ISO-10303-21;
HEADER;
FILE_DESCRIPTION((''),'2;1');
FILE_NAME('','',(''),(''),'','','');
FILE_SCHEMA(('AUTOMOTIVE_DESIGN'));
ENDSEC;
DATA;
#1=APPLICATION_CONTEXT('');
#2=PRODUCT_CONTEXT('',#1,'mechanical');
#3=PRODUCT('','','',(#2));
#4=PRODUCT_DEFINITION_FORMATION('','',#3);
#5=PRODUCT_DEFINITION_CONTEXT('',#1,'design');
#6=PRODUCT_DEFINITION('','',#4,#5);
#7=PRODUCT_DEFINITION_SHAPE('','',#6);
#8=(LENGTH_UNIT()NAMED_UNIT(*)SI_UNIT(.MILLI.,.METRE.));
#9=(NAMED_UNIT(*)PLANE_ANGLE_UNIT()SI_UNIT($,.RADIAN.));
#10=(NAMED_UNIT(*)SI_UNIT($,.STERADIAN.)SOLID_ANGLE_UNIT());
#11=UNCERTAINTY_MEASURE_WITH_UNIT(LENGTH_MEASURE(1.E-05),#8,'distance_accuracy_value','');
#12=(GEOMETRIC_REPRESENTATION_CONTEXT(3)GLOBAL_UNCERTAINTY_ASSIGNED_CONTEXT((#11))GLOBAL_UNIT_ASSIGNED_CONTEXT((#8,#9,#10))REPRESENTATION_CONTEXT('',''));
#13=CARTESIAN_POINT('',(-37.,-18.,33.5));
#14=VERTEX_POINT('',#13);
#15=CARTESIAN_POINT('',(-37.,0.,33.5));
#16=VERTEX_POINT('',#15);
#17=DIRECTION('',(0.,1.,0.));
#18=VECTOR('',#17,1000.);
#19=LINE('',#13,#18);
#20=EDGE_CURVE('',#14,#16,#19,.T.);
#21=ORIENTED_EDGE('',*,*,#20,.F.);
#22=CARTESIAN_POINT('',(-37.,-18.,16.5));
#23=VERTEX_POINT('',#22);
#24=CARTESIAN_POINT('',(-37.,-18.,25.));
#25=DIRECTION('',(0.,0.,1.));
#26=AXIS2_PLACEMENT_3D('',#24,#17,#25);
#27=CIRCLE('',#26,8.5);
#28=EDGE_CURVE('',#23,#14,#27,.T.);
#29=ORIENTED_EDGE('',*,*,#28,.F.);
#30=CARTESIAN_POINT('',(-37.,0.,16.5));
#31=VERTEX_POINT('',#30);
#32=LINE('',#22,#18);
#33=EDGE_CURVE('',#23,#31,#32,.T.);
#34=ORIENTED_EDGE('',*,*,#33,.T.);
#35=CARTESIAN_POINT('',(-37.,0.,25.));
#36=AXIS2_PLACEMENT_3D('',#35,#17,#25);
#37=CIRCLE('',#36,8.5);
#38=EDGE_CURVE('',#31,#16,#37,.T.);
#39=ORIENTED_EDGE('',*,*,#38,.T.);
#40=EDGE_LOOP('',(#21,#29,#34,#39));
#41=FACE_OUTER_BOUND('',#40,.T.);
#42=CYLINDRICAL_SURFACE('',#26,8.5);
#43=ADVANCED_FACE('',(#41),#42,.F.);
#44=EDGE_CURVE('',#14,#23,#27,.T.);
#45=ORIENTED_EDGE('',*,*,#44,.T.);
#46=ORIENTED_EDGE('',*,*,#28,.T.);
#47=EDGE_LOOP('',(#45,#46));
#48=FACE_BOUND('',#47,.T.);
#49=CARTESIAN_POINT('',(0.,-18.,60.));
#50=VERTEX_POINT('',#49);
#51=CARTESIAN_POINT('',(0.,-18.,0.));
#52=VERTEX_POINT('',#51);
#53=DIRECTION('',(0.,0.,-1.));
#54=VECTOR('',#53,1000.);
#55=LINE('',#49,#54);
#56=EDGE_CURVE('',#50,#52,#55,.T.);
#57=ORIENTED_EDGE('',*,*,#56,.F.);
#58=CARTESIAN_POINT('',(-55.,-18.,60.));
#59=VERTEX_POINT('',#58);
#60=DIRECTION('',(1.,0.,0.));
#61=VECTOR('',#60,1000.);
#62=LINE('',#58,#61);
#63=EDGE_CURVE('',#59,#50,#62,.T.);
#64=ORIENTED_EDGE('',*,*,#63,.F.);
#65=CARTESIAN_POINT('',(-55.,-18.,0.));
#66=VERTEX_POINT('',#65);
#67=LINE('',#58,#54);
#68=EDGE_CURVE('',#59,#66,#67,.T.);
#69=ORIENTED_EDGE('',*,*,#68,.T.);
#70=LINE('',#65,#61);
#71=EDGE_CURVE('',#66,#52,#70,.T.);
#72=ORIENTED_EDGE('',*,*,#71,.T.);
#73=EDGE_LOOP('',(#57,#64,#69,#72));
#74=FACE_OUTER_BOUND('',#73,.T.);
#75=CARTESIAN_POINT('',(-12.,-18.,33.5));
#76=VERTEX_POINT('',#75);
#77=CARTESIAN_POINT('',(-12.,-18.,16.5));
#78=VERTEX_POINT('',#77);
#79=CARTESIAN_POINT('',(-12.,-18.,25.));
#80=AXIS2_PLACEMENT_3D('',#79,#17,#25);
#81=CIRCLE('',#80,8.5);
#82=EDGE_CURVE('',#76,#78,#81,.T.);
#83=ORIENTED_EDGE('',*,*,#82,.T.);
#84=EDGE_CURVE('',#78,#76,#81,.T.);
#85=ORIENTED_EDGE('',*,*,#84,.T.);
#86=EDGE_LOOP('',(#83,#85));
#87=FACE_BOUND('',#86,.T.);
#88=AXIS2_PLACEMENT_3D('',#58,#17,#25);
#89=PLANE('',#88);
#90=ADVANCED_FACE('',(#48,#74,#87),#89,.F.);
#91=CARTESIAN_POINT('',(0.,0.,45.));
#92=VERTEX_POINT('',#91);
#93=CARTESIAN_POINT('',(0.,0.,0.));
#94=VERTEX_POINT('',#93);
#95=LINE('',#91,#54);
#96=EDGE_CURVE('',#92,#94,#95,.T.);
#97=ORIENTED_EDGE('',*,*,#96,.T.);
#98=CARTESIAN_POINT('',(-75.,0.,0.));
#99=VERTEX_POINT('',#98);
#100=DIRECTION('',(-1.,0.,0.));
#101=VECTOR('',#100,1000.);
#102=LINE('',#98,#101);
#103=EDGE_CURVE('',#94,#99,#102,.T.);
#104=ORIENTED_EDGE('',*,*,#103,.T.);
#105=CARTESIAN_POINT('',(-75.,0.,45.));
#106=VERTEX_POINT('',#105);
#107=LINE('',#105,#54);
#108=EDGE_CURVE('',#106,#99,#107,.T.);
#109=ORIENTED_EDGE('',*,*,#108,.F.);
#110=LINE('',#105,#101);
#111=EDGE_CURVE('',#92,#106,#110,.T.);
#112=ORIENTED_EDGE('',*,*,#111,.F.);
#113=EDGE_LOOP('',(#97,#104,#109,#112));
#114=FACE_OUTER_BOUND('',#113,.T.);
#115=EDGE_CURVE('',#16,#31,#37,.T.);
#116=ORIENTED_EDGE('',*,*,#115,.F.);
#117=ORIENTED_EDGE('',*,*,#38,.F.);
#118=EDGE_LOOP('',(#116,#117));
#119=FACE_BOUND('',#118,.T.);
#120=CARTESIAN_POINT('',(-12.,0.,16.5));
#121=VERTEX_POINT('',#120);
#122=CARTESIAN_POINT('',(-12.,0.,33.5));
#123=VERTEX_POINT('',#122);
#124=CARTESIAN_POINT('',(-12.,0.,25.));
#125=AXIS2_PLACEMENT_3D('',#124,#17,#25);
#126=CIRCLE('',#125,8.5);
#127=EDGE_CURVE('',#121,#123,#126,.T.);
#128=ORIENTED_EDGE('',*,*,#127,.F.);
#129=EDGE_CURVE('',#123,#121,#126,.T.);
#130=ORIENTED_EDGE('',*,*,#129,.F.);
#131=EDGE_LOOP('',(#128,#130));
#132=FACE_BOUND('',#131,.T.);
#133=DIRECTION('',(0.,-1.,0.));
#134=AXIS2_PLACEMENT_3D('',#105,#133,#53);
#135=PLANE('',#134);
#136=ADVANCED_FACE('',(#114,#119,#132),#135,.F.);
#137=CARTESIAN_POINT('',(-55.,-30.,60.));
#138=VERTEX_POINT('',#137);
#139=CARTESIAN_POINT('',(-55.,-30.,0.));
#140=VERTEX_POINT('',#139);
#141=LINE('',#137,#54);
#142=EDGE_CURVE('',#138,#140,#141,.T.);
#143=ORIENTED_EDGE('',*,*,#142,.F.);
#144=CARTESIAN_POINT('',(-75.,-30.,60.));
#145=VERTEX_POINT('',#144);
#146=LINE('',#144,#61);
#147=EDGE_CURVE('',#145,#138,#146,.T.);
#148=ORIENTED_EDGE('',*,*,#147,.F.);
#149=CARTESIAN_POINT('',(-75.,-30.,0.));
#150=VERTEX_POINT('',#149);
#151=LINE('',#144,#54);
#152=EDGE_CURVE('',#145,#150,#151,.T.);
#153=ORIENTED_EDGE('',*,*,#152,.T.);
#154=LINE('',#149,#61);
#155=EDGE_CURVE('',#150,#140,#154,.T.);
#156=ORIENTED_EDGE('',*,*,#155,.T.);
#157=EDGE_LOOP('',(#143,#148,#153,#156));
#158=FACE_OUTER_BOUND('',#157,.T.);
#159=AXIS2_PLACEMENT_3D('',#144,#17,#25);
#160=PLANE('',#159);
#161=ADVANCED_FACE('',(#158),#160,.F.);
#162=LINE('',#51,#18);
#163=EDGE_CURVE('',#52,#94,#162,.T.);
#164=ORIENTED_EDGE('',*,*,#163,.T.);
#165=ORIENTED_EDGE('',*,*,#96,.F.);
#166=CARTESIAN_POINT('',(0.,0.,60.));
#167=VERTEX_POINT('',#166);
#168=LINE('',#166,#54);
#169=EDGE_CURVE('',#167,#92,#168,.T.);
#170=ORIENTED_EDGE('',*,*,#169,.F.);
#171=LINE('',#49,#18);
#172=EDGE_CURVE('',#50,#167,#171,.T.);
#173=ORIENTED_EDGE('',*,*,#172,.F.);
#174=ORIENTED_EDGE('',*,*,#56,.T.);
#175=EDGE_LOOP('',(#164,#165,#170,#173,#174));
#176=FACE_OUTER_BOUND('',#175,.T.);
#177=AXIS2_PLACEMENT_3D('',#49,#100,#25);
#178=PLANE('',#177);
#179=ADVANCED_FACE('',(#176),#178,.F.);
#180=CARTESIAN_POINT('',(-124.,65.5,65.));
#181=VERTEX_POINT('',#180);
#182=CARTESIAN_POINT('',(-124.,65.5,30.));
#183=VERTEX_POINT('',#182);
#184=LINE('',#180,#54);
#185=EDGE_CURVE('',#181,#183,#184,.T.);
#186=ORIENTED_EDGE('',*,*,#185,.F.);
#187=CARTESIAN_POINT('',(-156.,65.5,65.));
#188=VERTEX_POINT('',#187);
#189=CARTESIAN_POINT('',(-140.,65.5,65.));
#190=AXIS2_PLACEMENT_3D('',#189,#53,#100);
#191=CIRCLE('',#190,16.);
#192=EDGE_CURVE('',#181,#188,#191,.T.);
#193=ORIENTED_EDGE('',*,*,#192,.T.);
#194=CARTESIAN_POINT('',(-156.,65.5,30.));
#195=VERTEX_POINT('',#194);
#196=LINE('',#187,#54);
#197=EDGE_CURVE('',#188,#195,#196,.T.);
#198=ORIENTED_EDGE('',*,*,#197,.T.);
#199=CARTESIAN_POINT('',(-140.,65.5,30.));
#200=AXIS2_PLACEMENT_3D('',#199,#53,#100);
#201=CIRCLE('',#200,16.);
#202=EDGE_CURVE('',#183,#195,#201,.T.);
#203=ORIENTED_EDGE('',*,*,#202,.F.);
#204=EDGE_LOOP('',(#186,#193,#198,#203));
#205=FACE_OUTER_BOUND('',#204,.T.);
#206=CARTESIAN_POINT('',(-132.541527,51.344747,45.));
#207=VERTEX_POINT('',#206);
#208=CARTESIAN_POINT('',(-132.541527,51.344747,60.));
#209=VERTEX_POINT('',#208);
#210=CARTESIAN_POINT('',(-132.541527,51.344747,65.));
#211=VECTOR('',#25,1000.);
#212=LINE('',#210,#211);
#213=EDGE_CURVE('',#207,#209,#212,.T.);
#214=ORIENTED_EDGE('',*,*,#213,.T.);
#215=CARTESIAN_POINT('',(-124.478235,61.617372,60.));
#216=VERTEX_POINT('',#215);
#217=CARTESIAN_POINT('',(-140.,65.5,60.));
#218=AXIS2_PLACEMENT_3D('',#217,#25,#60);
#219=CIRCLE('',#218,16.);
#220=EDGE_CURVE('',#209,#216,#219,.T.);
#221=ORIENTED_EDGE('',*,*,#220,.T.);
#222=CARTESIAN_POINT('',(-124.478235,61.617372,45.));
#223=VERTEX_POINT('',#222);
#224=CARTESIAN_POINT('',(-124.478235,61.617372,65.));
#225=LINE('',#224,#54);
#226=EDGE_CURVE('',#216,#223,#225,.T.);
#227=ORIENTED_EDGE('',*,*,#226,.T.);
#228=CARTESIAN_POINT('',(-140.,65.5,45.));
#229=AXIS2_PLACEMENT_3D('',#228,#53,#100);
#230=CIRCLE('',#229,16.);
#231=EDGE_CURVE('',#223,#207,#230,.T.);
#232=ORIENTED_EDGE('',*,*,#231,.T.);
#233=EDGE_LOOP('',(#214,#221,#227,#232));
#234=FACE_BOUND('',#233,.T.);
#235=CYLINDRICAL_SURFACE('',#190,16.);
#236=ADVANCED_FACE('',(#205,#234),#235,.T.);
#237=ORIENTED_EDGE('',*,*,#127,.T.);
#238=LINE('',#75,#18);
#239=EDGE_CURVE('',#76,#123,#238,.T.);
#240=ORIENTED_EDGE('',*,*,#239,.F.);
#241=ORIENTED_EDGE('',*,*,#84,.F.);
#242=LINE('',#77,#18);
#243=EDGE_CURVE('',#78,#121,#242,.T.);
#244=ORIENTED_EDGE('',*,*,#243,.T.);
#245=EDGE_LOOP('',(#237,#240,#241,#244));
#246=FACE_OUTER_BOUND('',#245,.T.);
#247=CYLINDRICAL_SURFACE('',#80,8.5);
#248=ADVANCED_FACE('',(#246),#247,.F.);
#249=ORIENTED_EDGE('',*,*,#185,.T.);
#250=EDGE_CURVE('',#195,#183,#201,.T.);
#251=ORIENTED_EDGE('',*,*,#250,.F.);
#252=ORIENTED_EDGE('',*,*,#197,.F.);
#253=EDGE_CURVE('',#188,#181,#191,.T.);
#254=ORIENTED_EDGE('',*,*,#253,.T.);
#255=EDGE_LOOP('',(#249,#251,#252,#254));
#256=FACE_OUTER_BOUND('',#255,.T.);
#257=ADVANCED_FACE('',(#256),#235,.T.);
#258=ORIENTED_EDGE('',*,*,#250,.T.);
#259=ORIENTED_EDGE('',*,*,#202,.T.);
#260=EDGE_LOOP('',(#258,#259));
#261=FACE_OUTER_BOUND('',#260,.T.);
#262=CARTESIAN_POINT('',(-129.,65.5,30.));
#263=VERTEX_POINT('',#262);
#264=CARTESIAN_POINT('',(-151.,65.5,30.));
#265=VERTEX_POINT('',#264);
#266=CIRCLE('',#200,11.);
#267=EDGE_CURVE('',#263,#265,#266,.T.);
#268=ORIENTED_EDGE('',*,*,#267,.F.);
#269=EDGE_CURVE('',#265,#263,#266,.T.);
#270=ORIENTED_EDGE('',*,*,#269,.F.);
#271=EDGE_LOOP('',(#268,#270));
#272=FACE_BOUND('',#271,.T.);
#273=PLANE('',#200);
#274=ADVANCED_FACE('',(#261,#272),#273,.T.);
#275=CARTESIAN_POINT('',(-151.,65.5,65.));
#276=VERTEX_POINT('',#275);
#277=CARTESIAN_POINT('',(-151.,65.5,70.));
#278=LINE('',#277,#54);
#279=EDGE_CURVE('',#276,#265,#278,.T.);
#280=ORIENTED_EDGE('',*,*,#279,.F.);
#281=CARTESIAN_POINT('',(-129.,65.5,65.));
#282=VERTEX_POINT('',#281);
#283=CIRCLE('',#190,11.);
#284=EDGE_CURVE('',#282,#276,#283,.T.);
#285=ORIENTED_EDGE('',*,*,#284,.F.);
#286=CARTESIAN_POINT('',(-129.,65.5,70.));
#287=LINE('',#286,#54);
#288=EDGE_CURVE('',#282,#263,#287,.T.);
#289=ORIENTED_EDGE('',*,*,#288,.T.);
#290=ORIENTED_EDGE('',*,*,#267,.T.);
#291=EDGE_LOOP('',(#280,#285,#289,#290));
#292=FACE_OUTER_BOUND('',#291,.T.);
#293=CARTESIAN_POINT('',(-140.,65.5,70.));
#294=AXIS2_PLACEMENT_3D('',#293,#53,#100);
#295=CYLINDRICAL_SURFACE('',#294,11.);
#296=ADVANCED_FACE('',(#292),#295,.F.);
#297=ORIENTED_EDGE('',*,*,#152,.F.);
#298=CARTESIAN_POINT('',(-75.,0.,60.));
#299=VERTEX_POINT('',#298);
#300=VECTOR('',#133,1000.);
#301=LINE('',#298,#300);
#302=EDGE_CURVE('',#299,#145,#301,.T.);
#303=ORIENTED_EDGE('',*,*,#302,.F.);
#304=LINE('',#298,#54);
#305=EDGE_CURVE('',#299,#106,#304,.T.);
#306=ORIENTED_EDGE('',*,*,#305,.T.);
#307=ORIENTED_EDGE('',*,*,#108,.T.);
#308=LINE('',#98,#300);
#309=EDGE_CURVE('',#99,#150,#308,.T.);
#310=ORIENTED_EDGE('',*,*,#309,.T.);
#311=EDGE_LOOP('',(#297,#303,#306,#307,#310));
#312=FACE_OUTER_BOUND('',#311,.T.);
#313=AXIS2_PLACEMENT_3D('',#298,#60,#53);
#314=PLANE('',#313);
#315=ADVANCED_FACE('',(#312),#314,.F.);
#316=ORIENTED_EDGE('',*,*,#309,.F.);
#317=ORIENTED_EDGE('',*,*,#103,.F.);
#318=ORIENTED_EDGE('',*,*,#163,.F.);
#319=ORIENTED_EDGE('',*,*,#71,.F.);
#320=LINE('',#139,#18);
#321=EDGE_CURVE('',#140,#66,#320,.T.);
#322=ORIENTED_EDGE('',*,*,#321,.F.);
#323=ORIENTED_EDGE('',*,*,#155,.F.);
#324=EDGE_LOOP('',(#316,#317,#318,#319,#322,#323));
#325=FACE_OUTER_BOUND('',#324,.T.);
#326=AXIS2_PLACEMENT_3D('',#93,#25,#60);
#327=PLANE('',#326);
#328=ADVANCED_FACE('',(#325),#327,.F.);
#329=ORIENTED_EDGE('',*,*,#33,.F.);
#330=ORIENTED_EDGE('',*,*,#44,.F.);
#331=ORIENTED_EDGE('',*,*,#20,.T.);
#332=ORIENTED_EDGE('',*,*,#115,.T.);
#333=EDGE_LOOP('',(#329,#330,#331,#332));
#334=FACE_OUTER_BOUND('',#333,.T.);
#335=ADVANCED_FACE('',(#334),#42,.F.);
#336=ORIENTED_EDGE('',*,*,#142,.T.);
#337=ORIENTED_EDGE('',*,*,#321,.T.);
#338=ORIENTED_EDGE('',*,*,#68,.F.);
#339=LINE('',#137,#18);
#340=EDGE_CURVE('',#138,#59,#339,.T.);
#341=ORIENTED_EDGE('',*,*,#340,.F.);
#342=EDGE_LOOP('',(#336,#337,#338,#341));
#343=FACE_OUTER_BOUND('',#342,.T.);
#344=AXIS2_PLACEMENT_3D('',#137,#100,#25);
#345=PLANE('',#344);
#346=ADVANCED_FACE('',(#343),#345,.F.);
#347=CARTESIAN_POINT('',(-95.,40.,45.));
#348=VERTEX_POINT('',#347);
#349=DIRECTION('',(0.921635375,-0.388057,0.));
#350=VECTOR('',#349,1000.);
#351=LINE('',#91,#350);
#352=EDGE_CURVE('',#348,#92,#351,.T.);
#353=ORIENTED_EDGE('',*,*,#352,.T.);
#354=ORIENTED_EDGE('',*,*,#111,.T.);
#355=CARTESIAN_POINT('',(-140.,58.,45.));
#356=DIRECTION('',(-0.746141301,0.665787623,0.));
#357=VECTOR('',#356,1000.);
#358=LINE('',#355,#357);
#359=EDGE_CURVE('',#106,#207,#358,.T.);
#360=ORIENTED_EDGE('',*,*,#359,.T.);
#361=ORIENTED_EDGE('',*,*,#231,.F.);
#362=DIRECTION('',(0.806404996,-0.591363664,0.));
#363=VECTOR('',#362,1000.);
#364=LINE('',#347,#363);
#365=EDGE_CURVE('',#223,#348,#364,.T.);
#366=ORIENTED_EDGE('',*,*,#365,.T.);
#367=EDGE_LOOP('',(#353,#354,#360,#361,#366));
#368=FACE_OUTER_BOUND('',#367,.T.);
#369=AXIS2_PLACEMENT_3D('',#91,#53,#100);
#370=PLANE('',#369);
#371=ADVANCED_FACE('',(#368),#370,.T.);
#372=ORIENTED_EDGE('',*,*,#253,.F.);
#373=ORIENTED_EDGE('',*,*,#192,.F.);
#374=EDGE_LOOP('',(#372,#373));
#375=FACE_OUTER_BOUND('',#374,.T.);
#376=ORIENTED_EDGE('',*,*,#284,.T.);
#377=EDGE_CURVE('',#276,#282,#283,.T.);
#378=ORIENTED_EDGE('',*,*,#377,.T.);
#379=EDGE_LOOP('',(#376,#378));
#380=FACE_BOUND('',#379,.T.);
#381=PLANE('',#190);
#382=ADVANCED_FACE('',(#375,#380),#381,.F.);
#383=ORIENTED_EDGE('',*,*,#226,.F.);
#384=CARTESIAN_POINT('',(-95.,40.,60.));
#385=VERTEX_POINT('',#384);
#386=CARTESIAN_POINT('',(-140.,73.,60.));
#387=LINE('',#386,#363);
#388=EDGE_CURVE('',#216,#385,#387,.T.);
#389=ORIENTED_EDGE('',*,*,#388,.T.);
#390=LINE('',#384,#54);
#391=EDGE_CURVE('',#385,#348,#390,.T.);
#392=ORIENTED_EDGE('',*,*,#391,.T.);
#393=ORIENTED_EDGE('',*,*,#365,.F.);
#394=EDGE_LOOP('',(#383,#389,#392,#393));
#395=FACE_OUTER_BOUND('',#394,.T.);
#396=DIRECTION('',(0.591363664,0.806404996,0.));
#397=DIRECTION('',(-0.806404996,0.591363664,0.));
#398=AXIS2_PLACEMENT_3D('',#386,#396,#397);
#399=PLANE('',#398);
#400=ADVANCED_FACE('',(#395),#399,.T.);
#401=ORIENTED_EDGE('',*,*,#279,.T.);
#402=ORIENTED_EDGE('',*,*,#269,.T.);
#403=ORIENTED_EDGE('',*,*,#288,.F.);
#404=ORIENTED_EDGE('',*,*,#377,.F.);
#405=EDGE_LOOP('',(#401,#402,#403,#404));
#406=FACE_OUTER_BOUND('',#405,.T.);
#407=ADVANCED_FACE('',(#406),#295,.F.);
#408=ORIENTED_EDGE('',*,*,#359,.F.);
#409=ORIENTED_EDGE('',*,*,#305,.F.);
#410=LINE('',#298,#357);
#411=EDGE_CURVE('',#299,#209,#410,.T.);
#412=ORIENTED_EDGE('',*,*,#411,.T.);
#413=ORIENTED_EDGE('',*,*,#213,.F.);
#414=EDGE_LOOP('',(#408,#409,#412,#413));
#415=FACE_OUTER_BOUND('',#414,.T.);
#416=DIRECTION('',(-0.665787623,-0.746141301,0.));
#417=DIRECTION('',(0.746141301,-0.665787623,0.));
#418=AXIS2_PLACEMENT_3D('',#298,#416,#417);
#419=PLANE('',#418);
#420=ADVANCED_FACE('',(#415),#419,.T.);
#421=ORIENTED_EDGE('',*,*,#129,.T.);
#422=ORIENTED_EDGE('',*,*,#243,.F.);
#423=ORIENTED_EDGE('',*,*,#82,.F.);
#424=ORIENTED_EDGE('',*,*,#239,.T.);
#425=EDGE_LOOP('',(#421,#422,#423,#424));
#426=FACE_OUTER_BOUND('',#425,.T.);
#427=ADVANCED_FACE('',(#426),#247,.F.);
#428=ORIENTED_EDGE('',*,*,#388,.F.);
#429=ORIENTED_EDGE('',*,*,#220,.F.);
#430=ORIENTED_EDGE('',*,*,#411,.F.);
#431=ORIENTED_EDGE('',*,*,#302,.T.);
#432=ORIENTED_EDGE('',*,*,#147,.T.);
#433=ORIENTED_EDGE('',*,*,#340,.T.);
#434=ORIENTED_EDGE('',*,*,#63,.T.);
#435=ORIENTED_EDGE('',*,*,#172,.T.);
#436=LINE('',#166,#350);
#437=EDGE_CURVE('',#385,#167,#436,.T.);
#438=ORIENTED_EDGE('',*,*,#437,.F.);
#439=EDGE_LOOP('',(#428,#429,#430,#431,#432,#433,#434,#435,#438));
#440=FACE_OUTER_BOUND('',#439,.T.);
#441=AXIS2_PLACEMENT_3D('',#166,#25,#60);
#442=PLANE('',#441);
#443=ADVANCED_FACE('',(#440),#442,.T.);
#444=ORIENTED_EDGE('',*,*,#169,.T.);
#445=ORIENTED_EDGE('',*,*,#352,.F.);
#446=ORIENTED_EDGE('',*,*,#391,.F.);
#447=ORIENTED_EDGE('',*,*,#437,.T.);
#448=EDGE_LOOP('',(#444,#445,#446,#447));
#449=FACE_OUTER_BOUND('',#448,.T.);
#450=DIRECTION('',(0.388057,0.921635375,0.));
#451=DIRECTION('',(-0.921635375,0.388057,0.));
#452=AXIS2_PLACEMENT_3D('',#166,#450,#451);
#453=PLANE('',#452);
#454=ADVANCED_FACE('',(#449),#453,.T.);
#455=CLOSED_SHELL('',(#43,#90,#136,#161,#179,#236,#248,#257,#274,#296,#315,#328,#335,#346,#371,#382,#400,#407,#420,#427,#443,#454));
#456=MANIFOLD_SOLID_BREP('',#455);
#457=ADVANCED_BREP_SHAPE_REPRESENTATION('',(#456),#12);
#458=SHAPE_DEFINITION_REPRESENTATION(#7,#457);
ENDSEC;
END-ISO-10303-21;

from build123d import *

# Parameters (mm, degrees)
BASE_BLOCK_DEPTH           = 60
ARM_DEPTH                  = 60
ARM_TRIM_CUT_DEPTH         = 45
HUB_SKETCH_32_R            = 16
HUB_32_DEPTH               = 20
HUB_START                  = 15
HUB_EXTENSION_SKETCH_32_R  = 16
HUB_EXTENSION_32_DEPTH     = 15
BORE_SKETCH_22_R           = 11
HUB_BORE_22_DEPTH          = 40
MOUNTING_HOLES_SKETCH_R    = 8.5
MOUNTING_HOLES_2X_17_DEPTH = 18


with BuildPart() as part:
    # Base Profile Sketch → Base Block (new body)
    with BuildSketch(Plane.XY):
        Polygon((0, 0), (-75, 0), (-75, -30), (-55, -30), (-55, -18), (0, -18), align=None)
    extrude(amount=BASE_BLOCK_DEPTH)

    # Arm Profile Sketch → Arm (add)
    with BuildSketch(Plane(origin=(0, 0, 0), x_dir=(-1, 0, 0), z_dir=(0, 0, -1))):
        Polygon((0, 0), (75, 0), (140, 58), (140, 73), (95, 40), align=None)
    extrude(amount=-ARM_DEPTH)

    # Arm Trim Sketch → Arm Trim Cut (cut)
    with BuildSketch(Plane(origin=(0, 0, 0), x_dir=(-1, 0, 0), z_dir=(0, 0, -1))):
        Polygon((0, 0), (95, 40), (140, 73), (140, 58), (75, 0), align=None)
    extrude(amount=-ARM_TRIM_CUT_DEPTH, mode=Mode.SUBTRACT)

    # Hub Sketch Ø32 → Hub Ø32 (add)
    with BuildSketch(Plane(origin=(0, 0, 45), x_dir=(-1, 0, 0), z_dir=(0, 0, -1))):
        with Locations((140, 65.5)):
            Circle(HUB_SKETCH_32_R)
    extrude(amount=-HUB_32_DEPTH)

    # Hub Extension Sketch Ø32 → Hub Extension Ø32 (add)
    with BuildSketch(Plane(origin=(0, 0, 45), x_dir=(-1, 0, 0), z_dir=(0, 0, -1)).offset(HUB_START)):
        with Locations((140, 65.5)):
            Circle(HUB_EXTENSION_SKETCH_32_R)
    extrude(amount=-HUB_EXTENSION_32_DEPTH)

    # Bore Sketch Ø22 → Hub Bore Ø22 (cut)
    with BuildSketch(Plane(origin=(0, 0, 30), x_dir=(-1, 0, 0), z_dir=(0, 0, -1))):
        with Locations((140, 65.5)):
            Circle(BORE_SKETCH_22_R)
    extrude(amount=-HUB_BORE_22_DEPTH, mode=Mode.SUBTRACT)

    # Mounting Holes Sketch → Mounting Holes 2xØ17 (cut)
    with BuildSketch(Plane(origin=(0, 0, 0), x_dir=(1, 0, 0), z_dir=(0, 1, 0))):
        with Locations(Location((-12, -25, 0), (0, 0, 270))):
            Circle(MOUNTING_HOLES_SKETCH_R)
        with Locations(Location((-37, -25, 0), (0, 0, 270))):
            Circle(MOUNTING_HOLES_SKETCH_R)
    extrude(amount=-MOUNTING_HOLES_2X_17_DEPTH, mode=Mode.SUBTRACT)


solid = part.part
